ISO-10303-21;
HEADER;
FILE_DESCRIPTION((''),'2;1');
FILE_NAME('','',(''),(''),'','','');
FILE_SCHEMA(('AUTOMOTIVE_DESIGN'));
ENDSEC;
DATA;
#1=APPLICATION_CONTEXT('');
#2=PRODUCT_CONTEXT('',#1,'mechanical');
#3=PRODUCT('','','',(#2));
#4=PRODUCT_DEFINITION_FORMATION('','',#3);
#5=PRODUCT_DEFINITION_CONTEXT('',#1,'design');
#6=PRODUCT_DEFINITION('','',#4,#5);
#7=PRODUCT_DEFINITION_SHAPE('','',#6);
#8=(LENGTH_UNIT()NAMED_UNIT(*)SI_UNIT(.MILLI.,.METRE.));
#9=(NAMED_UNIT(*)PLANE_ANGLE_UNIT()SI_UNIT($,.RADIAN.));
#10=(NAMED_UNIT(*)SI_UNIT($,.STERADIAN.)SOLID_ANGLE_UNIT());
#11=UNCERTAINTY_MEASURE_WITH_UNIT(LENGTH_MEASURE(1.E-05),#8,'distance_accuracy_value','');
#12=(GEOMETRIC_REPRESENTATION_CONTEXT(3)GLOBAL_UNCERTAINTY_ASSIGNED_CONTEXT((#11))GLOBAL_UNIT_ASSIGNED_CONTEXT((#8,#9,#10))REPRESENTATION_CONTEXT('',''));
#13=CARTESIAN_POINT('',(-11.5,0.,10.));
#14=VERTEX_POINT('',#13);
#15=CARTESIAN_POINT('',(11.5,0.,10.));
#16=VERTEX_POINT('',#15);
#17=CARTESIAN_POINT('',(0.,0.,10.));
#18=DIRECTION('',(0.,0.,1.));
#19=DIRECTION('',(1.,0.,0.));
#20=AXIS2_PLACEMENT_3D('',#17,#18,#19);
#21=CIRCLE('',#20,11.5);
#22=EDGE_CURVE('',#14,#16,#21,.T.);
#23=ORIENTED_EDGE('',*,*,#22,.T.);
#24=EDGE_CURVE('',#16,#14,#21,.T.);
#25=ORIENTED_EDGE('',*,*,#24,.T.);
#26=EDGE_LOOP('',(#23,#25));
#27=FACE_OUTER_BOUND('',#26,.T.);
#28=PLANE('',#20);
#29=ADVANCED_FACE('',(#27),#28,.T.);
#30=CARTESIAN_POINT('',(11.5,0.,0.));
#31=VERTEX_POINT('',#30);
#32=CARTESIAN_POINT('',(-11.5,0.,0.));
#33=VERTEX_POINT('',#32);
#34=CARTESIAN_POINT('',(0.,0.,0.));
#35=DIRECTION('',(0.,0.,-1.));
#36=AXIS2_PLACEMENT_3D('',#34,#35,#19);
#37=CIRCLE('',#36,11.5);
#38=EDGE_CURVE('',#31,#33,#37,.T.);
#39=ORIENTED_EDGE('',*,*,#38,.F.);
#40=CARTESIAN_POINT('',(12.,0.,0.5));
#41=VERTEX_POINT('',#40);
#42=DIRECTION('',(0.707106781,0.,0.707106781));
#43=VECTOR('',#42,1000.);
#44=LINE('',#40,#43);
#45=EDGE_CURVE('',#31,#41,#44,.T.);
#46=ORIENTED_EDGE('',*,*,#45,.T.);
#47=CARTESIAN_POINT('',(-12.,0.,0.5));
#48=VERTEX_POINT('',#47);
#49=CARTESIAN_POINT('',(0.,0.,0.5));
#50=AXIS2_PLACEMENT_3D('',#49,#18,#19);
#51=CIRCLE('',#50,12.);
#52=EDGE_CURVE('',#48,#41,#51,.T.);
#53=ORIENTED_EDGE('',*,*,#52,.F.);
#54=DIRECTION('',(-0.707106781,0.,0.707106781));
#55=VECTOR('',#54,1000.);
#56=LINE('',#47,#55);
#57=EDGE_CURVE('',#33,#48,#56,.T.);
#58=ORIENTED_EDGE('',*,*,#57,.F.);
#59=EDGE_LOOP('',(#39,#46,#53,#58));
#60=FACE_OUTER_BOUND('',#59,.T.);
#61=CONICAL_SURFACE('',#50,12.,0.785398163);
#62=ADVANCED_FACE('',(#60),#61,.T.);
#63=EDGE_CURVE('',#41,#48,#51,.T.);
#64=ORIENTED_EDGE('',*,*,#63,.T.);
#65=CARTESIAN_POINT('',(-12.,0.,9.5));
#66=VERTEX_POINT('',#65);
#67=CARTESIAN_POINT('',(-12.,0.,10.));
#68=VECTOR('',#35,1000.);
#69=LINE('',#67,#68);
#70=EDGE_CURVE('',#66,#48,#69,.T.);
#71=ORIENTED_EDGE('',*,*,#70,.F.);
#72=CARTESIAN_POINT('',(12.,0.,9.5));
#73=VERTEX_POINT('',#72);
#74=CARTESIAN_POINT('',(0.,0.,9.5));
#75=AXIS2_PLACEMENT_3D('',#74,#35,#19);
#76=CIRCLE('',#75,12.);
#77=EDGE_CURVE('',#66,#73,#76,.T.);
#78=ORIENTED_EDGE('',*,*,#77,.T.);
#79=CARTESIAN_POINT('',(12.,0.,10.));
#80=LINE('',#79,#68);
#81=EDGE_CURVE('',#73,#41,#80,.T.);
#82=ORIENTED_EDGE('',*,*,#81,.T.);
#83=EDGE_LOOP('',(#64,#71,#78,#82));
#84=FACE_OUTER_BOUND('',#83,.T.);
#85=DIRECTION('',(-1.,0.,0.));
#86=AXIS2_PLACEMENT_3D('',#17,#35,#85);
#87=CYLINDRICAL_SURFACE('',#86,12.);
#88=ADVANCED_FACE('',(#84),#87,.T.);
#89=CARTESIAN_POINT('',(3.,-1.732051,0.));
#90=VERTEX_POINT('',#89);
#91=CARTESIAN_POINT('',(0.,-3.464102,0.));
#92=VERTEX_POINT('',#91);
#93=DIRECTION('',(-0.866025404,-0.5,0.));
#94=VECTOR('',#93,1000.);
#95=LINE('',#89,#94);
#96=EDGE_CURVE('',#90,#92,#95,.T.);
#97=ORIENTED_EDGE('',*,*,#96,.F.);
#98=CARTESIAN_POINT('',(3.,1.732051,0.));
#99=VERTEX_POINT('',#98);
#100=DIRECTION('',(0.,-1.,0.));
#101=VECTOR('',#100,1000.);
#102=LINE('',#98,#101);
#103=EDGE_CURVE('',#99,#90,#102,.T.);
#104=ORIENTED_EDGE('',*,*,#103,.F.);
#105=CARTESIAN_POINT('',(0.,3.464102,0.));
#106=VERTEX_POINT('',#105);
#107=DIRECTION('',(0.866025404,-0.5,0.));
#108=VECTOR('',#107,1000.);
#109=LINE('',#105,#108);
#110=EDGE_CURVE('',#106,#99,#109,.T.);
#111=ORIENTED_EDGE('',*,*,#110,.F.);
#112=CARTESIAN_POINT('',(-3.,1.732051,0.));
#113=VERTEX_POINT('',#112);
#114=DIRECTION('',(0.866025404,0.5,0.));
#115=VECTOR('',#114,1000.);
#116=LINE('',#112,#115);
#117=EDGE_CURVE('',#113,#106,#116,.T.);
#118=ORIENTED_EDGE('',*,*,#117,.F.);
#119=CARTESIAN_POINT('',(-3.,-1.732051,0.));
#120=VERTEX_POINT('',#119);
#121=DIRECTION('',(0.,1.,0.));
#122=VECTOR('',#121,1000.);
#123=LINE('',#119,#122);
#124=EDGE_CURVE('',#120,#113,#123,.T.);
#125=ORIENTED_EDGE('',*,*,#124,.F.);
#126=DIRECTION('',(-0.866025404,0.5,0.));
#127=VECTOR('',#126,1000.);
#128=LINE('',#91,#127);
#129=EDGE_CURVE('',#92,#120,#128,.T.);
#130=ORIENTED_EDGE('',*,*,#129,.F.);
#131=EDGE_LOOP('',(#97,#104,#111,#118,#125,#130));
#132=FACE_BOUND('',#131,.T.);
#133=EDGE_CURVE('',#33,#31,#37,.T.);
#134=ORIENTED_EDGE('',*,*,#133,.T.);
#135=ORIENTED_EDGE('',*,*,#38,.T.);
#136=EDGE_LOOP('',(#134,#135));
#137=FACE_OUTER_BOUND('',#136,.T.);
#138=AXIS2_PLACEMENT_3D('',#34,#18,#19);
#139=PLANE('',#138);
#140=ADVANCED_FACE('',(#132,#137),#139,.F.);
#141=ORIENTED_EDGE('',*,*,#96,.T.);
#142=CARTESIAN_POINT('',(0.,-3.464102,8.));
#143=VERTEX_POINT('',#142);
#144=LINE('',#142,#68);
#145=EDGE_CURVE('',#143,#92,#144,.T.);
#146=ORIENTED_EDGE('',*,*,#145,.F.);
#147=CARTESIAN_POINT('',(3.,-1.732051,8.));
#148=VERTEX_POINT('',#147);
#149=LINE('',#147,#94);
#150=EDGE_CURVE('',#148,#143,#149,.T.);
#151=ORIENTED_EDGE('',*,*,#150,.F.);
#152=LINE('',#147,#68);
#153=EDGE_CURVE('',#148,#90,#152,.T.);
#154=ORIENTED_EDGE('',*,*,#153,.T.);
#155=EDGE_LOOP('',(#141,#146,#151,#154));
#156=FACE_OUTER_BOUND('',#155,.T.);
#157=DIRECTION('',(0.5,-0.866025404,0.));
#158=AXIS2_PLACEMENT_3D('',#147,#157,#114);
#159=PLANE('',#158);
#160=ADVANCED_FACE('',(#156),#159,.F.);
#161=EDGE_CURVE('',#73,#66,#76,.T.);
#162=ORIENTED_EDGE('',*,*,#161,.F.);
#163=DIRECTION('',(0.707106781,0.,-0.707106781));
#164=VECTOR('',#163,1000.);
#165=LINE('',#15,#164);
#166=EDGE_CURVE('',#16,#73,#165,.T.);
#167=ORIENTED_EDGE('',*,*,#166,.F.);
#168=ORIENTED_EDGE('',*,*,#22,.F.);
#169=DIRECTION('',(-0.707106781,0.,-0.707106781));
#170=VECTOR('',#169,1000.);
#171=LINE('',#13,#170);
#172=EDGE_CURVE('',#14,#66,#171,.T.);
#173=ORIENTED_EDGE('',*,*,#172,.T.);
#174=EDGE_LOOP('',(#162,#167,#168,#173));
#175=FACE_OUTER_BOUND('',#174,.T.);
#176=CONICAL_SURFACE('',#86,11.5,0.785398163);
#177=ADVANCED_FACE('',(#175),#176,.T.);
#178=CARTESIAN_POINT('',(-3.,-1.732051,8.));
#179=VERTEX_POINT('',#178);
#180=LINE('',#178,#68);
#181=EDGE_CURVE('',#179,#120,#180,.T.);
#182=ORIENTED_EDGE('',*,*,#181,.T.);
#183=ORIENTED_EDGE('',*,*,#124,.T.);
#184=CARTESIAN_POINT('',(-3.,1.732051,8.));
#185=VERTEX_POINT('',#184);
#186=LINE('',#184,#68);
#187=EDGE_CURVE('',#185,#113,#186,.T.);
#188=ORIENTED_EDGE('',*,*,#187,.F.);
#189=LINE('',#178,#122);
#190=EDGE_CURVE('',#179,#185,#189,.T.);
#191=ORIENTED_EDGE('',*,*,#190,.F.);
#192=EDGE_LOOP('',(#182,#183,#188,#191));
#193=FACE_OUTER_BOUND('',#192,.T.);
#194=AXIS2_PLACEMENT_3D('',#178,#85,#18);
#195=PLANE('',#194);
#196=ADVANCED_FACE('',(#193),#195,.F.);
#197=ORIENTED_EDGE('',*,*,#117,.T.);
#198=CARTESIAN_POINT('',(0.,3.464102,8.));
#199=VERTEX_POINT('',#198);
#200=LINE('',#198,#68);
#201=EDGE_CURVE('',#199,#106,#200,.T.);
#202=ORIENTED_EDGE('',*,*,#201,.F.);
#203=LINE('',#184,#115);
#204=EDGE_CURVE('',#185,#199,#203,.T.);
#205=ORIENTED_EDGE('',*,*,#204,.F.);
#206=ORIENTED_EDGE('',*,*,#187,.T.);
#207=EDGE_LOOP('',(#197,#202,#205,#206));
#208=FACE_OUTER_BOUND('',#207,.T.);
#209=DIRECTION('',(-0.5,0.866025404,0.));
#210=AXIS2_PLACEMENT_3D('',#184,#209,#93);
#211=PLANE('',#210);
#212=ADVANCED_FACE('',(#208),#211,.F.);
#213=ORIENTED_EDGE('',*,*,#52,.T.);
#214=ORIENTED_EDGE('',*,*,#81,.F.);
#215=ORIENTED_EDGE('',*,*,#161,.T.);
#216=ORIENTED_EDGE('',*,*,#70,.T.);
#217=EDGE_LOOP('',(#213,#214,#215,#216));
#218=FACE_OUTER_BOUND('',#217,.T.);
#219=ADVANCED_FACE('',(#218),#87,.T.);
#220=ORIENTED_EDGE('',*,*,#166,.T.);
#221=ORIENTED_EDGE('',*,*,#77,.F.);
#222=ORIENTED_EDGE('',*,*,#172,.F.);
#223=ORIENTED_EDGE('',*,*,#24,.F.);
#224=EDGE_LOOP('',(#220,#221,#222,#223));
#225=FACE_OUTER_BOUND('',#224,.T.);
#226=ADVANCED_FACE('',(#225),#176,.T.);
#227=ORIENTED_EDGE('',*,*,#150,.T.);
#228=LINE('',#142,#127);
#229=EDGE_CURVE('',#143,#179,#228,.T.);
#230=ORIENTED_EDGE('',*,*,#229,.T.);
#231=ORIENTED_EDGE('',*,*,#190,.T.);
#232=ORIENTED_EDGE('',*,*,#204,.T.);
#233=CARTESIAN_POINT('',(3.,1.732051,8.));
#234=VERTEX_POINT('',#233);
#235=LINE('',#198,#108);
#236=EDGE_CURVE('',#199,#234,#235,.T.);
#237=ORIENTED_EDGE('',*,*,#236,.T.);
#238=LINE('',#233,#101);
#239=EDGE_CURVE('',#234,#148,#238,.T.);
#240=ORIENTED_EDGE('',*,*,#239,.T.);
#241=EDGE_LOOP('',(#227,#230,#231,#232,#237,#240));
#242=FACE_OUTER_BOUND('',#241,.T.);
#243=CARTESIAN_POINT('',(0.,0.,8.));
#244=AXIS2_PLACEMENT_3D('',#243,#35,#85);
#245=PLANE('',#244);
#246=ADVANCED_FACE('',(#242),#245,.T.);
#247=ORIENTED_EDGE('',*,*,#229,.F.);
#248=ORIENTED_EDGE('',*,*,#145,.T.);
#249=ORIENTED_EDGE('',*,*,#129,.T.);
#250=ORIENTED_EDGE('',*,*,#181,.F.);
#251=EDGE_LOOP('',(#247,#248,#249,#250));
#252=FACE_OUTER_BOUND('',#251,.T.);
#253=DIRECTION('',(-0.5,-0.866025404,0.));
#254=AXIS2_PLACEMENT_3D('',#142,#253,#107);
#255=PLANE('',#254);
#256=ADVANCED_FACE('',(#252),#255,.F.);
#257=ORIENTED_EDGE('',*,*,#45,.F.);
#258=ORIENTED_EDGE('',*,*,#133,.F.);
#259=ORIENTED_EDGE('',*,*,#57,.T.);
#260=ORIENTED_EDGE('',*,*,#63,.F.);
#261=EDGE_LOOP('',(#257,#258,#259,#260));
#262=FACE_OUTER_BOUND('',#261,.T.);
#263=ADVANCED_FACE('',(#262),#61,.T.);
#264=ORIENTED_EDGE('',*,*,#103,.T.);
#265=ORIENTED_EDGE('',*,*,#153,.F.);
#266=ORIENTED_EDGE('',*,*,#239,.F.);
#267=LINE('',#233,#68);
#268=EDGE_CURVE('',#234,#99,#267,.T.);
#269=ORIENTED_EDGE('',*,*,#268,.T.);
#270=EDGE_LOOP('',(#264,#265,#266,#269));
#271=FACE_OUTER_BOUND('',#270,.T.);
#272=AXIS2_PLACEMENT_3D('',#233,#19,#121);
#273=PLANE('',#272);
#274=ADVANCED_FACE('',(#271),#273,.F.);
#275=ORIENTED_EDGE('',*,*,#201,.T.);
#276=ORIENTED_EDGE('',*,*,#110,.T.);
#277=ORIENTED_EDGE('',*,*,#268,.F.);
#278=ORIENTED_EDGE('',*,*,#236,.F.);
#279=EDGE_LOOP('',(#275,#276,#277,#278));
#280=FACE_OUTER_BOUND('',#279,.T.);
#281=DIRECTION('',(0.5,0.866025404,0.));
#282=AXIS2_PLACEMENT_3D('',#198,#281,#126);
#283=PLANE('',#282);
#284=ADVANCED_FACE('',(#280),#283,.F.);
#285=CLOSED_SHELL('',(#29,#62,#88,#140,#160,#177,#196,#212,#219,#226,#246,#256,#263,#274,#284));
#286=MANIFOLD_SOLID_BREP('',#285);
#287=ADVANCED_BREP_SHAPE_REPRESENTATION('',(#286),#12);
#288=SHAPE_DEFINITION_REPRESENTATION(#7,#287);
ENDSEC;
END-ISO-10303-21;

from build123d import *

# Parameters (mm, degrees)
SKETCH_1_R          = 12
EXTRUDE_1_DEPTH     = 10
CHAMFER_1_SIZE      = 0.5
CUT_EXTRUDE_1_DEPTH = 8


with BuildPart() as part:
    # 草图1 → 凸台-拉伸1 (new body)
    with BuildSketch(Plane.XY):
        Circle(SKETCH_1_R)
    extrude(amount=EXTRUDE_1_DEPTH)

    # 倒角1
    chamfer_1_edges = [part.edges().sort_by_distance(p)[0] for p in [
        (-12, 0, 0),
        (-12, 0, 10),
    ]]
    chamfer(chamfer_1_edges, length=CHAMFER_1_SIZE)

    # 草图2 → 切除-拉伸1 (cut)
    with BuildSketch(Plane(origin=(0, 0, 0), x_dir=(-1, 0, 0), z_dir=(0, 0, -1))):
        Polygon((0, -3.464101615), (3, -1.732050808), (3, 1.732050808), (0, 3.464101615), (-3, 1.732050808), (-3, -1.732050808), align=None)
    extrude(amount=-CUT_EXTRUDE_1_DEPTH, mode=Mode.SUBTRACT)


solid = part.part
